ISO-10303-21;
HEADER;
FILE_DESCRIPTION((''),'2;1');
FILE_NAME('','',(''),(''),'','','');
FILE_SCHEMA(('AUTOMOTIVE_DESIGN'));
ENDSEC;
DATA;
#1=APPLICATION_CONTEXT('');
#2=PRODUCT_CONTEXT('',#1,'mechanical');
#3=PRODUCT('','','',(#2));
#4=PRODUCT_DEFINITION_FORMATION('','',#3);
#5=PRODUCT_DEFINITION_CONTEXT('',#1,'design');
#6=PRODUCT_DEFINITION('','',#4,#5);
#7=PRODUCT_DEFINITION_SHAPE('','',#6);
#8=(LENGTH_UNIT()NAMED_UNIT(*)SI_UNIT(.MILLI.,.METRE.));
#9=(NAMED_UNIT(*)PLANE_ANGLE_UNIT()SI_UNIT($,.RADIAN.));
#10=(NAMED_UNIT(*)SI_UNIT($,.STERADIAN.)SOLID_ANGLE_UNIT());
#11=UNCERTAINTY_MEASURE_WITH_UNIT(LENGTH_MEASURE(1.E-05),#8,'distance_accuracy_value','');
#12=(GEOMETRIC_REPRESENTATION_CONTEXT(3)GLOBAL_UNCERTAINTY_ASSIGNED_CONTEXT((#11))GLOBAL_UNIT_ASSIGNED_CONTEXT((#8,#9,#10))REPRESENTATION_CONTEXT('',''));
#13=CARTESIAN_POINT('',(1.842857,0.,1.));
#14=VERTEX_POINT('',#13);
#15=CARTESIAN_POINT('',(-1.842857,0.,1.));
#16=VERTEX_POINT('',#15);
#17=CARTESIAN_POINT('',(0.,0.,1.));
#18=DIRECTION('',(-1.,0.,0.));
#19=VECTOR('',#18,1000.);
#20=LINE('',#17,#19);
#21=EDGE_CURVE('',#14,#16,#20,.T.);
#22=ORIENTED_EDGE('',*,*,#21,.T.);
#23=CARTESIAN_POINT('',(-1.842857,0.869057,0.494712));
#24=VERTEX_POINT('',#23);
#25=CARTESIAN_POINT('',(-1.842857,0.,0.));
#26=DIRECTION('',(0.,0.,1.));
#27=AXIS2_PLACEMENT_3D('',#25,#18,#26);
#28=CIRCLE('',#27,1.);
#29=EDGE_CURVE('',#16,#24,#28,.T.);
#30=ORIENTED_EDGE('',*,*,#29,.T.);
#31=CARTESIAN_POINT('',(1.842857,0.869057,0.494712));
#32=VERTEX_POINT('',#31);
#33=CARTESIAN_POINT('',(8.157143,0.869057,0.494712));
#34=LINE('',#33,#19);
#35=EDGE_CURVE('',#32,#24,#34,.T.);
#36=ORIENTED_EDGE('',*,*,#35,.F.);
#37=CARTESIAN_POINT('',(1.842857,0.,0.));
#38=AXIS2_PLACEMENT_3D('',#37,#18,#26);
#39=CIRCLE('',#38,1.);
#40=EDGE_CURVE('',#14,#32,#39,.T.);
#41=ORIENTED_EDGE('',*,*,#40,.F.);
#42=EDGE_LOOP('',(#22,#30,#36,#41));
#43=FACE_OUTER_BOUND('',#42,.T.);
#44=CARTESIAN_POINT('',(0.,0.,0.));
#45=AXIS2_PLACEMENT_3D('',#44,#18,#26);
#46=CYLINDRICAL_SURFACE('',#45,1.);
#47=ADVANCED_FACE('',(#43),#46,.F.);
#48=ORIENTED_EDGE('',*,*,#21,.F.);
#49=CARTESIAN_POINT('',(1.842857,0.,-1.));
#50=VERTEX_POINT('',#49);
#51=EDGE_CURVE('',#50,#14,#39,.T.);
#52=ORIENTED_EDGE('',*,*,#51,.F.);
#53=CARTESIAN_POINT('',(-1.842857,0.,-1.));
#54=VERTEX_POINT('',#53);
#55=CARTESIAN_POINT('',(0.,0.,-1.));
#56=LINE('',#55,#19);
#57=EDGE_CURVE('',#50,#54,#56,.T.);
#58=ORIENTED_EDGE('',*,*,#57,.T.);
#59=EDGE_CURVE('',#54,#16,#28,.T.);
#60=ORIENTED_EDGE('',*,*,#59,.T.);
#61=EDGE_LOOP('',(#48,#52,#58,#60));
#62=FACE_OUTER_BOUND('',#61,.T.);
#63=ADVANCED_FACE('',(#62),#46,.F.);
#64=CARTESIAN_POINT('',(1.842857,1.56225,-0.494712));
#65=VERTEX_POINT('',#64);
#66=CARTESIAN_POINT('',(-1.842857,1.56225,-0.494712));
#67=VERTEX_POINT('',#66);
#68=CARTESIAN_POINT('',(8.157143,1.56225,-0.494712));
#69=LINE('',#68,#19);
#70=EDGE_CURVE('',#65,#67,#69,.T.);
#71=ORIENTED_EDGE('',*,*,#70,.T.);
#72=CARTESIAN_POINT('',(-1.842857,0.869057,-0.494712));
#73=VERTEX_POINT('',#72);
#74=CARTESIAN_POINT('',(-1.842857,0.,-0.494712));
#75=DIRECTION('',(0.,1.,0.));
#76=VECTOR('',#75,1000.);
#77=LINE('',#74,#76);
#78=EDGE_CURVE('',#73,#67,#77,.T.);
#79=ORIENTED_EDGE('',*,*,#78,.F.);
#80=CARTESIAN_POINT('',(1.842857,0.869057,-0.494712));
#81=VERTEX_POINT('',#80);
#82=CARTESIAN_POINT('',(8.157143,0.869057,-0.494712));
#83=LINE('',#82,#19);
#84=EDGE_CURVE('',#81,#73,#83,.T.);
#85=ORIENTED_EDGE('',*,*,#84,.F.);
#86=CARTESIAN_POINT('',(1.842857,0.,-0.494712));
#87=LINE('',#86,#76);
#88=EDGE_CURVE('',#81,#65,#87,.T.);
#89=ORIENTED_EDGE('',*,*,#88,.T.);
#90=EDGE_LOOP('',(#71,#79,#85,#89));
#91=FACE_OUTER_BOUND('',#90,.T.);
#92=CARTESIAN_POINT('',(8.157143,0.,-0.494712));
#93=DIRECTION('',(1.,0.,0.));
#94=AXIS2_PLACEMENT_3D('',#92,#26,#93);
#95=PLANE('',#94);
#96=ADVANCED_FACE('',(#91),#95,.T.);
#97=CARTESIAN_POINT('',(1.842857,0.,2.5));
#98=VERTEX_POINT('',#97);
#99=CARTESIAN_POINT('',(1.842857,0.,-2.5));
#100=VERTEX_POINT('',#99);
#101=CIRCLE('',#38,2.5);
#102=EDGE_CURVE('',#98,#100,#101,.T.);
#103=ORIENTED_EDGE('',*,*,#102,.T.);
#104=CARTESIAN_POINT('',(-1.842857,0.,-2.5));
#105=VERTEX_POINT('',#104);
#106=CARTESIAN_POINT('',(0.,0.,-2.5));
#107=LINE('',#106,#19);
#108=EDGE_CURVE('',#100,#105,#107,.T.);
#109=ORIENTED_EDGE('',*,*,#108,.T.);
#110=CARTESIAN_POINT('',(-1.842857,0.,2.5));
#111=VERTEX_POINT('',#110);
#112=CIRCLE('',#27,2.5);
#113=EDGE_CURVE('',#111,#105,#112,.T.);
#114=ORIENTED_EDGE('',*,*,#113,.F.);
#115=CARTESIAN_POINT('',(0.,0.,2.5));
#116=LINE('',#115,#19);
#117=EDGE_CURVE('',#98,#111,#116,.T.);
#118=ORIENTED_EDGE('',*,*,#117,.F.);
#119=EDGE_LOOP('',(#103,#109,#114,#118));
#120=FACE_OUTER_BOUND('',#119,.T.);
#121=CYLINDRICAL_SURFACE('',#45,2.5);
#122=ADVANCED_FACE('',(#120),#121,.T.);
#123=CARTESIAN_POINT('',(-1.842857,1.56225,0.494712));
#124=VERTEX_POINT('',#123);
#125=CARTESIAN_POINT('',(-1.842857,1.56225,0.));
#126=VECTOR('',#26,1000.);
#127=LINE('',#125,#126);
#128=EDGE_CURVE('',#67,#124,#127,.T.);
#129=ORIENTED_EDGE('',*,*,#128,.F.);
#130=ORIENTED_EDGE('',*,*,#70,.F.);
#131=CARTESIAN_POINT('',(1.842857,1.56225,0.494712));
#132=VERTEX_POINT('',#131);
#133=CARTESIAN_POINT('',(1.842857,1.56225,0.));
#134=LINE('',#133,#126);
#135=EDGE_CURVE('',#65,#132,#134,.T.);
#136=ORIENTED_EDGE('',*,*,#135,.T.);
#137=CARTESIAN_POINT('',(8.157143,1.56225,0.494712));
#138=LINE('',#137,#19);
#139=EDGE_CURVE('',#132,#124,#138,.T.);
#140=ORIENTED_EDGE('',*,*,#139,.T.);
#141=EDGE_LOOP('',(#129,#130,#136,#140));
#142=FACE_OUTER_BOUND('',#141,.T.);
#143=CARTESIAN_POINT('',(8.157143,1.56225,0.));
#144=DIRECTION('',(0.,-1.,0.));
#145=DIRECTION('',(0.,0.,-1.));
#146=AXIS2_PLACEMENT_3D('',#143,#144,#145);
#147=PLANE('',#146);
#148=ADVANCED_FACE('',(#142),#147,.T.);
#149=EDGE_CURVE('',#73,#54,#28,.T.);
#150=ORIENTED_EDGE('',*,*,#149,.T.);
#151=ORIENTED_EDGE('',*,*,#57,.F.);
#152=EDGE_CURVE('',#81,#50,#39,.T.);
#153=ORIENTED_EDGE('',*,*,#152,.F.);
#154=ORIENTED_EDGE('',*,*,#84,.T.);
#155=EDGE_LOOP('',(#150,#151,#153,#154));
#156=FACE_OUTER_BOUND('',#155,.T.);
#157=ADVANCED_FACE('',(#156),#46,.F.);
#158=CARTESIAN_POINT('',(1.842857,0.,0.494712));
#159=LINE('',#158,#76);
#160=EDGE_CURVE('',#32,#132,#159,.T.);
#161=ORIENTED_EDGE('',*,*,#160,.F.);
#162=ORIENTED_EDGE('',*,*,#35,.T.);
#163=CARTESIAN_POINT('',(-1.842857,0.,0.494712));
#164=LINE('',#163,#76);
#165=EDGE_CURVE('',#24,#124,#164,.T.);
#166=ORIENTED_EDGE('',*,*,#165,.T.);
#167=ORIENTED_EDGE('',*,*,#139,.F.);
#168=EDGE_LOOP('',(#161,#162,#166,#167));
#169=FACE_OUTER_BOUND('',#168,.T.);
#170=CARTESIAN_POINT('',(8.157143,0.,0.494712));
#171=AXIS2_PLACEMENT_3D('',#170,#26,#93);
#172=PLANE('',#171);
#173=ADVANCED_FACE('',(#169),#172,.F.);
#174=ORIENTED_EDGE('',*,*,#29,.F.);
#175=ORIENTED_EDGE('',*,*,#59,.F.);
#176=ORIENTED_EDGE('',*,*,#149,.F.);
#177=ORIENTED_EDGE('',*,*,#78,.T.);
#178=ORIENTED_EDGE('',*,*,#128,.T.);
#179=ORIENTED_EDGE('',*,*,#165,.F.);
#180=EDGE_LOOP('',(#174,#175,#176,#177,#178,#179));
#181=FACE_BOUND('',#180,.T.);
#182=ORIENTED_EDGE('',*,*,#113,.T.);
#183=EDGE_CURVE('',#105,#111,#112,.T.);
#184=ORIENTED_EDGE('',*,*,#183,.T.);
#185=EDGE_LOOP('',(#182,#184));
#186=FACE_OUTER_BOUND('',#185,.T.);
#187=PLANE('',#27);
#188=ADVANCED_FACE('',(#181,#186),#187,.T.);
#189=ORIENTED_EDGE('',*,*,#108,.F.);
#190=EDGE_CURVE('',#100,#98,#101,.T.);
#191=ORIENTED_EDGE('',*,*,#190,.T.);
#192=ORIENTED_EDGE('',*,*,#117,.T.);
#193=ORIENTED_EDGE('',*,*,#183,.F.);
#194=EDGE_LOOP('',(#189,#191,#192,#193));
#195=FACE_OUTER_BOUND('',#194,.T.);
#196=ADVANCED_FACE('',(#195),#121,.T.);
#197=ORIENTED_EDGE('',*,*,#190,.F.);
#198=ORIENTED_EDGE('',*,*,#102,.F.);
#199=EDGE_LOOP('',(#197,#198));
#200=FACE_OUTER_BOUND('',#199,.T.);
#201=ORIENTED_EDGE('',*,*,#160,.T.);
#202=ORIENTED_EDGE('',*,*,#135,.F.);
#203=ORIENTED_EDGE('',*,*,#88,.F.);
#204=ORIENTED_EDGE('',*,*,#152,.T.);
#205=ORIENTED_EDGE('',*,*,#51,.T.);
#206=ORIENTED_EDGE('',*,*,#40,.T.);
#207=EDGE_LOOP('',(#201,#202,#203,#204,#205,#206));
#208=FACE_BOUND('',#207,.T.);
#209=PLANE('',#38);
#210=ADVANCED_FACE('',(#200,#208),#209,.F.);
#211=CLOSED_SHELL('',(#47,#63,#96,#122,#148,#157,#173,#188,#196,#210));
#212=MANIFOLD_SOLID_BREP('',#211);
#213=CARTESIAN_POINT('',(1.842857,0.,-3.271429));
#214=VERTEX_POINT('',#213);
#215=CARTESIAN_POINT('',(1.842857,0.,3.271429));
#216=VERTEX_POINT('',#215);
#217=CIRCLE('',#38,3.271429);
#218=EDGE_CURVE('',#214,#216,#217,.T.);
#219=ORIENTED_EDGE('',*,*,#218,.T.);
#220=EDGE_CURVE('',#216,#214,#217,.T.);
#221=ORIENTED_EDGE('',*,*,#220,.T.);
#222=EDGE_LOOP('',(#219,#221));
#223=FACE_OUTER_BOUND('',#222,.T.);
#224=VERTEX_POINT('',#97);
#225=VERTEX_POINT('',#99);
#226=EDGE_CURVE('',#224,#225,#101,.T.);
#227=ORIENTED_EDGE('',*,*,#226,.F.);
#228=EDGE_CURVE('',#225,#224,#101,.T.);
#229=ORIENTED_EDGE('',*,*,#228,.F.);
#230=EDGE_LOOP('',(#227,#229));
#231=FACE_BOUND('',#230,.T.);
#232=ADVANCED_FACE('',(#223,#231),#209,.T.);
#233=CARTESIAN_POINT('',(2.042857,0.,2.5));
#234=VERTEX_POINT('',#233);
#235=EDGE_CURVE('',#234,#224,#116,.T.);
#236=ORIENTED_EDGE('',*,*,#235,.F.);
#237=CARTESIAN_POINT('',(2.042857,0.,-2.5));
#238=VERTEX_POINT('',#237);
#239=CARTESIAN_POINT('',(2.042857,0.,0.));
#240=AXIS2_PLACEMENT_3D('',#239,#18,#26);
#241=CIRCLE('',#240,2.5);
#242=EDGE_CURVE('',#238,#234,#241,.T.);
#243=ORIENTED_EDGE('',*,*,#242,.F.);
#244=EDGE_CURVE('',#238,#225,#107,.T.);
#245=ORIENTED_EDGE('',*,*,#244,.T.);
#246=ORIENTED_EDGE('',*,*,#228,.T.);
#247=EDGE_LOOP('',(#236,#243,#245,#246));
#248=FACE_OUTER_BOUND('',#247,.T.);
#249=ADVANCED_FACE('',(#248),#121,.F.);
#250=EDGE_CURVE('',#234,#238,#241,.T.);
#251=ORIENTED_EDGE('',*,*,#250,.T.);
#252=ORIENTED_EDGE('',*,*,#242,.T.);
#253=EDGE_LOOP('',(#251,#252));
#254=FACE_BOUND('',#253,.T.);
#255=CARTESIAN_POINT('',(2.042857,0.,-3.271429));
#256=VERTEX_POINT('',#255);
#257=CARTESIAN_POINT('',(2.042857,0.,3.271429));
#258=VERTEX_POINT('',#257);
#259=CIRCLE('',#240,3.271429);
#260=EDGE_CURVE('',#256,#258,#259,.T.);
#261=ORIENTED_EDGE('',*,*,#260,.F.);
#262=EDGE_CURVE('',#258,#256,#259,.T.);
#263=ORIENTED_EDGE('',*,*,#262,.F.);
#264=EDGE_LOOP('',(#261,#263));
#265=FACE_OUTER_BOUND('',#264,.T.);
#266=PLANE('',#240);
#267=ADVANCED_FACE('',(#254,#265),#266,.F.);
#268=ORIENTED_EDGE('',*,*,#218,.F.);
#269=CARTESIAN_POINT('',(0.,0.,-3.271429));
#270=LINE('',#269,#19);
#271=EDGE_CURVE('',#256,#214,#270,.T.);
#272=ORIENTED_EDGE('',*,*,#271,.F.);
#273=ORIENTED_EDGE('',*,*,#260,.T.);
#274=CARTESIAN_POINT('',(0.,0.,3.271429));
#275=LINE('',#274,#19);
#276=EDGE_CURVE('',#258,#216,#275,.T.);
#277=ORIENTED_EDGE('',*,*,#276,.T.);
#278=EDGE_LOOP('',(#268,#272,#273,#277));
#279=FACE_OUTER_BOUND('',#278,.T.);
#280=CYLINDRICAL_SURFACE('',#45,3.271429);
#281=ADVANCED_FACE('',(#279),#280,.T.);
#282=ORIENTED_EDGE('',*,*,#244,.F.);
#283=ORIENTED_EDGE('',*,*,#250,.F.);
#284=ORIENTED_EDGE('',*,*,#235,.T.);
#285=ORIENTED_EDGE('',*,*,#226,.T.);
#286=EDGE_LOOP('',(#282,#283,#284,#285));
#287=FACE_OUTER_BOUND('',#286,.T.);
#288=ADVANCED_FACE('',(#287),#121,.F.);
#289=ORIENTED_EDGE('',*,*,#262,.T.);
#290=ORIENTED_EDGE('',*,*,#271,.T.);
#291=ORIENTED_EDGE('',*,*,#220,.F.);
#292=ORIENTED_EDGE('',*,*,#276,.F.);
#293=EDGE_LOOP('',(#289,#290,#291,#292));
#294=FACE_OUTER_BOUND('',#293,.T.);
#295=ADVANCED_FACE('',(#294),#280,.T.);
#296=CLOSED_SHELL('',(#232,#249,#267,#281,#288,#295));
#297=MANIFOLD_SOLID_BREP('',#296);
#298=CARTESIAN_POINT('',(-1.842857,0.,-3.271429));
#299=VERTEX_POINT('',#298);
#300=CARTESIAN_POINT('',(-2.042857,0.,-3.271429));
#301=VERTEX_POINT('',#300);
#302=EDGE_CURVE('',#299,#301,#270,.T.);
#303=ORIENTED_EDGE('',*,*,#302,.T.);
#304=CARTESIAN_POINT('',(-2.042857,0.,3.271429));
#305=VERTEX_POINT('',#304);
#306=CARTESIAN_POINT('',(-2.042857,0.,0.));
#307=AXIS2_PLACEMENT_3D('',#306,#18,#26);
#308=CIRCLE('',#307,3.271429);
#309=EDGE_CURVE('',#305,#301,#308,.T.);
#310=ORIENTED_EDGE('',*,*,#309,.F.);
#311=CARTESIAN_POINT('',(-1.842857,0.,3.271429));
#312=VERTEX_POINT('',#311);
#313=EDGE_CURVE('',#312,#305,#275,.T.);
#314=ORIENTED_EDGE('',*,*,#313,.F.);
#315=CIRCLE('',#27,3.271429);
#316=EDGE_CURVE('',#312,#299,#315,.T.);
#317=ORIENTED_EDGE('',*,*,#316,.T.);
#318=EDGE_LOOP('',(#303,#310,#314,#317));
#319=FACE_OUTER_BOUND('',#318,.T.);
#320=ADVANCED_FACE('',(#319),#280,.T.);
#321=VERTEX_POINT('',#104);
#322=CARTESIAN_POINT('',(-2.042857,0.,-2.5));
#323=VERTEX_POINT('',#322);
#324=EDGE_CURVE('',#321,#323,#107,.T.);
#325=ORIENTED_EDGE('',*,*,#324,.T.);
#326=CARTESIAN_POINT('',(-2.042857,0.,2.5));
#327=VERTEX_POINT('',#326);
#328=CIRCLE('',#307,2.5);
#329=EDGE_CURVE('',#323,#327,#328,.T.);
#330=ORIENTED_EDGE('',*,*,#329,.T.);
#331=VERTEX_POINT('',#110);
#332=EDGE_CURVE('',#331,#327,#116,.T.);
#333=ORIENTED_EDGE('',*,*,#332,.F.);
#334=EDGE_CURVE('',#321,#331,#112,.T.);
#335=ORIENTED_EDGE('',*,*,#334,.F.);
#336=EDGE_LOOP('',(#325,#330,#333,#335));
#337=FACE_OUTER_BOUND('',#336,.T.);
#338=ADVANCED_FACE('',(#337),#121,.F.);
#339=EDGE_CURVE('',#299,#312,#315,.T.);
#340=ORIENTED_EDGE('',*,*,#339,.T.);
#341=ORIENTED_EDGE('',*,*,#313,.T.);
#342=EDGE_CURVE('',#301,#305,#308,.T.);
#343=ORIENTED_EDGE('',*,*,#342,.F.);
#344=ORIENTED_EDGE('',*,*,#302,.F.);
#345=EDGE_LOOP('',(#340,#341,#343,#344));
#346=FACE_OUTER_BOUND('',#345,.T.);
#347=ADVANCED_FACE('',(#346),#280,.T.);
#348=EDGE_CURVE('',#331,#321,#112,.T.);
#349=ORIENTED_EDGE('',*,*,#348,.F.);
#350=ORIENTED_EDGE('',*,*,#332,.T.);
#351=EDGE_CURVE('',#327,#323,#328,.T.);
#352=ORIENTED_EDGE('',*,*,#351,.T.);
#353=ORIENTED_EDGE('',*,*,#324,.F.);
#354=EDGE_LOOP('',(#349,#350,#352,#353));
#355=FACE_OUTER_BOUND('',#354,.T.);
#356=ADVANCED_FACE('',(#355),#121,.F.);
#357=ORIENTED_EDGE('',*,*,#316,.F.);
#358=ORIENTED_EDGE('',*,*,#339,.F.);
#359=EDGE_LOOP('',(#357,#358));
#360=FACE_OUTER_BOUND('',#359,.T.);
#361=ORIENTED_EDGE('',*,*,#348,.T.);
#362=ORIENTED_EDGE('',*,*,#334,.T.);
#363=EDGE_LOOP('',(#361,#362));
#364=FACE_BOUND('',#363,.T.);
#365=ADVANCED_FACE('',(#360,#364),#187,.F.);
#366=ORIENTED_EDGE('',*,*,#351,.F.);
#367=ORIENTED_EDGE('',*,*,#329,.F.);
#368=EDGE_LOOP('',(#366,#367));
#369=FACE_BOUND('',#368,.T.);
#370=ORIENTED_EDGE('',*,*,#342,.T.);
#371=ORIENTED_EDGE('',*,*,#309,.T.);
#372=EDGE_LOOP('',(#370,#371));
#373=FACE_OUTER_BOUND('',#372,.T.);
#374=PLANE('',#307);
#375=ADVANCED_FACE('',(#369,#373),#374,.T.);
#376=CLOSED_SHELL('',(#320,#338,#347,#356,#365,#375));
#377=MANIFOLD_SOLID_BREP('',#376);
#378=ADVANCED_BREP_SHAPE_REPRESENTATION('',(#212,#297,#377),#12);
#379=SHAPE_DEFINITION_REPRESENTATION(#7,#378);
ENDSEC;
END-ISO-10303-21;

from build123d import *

# Parameters (mm, degrees)
SKETCH1_W          = 3.685714286
SKETCH1_H          = 1.5
SKETCH1_W_2        = 0.2
SKETCH1_H_2        = 0.771428571
CUT_EXTRUDE1_START = -10
CUT_EXTRUDE1_DEPTH = 10


with BuildPart() as part:
    # Sketch1 → Revolve1 (revolve)
    with BuildSketch(Plane(origin=(0, 0, 0), x_dir=(1, 0, 0), z_dir=(0, 1, 0)), mode=Mode.PRIVATE) as revolve1_sk:
        with Locations((0, 1.75)):
            Rectangle(SKETCH1_W, SKETCH1_H)
        with Locations((1.942857143, 2.885714286)):
            Rectangle(SKETCH1_W_2, SKETCH1_H_2)
        with Locations((-1.942857143, 2.885714286)):
            Rectangle(SKETCH1_W_2, SKETCH1_H_2)
    revolve(revolve1_sk.sketch.rotate(Axis((0, 0, 0), (1, 0, 0)), 180), axis=Axis((0, 0, 0), (1, 0, 0)))

    # Sketch2 → Cut-Extrude1 (cut)
    with BuildSketch(Plane.ZY.offset(1.842857143).offset(CUT_EXTRUDE1_START)):
        with BuildLine():
            ThreePointArc((-0.494712466, 0.869056716), (0, 1), (0.494712466, 0.869056716))
            Line((0.494712466, 0.869056716), (0.494712466, 1.562249891))
            Line((0.494712466, 1.562249891), (-0.494712466, 1.562249891))
            Line((-0.494712466, 1.562249891), (-0.494712466, 0.869056716))
        make_face()
    extrude(amount=CUT_EXTRUDE1_DEPTH, mode=Mode.SUBTRACT)


solid = part.part
